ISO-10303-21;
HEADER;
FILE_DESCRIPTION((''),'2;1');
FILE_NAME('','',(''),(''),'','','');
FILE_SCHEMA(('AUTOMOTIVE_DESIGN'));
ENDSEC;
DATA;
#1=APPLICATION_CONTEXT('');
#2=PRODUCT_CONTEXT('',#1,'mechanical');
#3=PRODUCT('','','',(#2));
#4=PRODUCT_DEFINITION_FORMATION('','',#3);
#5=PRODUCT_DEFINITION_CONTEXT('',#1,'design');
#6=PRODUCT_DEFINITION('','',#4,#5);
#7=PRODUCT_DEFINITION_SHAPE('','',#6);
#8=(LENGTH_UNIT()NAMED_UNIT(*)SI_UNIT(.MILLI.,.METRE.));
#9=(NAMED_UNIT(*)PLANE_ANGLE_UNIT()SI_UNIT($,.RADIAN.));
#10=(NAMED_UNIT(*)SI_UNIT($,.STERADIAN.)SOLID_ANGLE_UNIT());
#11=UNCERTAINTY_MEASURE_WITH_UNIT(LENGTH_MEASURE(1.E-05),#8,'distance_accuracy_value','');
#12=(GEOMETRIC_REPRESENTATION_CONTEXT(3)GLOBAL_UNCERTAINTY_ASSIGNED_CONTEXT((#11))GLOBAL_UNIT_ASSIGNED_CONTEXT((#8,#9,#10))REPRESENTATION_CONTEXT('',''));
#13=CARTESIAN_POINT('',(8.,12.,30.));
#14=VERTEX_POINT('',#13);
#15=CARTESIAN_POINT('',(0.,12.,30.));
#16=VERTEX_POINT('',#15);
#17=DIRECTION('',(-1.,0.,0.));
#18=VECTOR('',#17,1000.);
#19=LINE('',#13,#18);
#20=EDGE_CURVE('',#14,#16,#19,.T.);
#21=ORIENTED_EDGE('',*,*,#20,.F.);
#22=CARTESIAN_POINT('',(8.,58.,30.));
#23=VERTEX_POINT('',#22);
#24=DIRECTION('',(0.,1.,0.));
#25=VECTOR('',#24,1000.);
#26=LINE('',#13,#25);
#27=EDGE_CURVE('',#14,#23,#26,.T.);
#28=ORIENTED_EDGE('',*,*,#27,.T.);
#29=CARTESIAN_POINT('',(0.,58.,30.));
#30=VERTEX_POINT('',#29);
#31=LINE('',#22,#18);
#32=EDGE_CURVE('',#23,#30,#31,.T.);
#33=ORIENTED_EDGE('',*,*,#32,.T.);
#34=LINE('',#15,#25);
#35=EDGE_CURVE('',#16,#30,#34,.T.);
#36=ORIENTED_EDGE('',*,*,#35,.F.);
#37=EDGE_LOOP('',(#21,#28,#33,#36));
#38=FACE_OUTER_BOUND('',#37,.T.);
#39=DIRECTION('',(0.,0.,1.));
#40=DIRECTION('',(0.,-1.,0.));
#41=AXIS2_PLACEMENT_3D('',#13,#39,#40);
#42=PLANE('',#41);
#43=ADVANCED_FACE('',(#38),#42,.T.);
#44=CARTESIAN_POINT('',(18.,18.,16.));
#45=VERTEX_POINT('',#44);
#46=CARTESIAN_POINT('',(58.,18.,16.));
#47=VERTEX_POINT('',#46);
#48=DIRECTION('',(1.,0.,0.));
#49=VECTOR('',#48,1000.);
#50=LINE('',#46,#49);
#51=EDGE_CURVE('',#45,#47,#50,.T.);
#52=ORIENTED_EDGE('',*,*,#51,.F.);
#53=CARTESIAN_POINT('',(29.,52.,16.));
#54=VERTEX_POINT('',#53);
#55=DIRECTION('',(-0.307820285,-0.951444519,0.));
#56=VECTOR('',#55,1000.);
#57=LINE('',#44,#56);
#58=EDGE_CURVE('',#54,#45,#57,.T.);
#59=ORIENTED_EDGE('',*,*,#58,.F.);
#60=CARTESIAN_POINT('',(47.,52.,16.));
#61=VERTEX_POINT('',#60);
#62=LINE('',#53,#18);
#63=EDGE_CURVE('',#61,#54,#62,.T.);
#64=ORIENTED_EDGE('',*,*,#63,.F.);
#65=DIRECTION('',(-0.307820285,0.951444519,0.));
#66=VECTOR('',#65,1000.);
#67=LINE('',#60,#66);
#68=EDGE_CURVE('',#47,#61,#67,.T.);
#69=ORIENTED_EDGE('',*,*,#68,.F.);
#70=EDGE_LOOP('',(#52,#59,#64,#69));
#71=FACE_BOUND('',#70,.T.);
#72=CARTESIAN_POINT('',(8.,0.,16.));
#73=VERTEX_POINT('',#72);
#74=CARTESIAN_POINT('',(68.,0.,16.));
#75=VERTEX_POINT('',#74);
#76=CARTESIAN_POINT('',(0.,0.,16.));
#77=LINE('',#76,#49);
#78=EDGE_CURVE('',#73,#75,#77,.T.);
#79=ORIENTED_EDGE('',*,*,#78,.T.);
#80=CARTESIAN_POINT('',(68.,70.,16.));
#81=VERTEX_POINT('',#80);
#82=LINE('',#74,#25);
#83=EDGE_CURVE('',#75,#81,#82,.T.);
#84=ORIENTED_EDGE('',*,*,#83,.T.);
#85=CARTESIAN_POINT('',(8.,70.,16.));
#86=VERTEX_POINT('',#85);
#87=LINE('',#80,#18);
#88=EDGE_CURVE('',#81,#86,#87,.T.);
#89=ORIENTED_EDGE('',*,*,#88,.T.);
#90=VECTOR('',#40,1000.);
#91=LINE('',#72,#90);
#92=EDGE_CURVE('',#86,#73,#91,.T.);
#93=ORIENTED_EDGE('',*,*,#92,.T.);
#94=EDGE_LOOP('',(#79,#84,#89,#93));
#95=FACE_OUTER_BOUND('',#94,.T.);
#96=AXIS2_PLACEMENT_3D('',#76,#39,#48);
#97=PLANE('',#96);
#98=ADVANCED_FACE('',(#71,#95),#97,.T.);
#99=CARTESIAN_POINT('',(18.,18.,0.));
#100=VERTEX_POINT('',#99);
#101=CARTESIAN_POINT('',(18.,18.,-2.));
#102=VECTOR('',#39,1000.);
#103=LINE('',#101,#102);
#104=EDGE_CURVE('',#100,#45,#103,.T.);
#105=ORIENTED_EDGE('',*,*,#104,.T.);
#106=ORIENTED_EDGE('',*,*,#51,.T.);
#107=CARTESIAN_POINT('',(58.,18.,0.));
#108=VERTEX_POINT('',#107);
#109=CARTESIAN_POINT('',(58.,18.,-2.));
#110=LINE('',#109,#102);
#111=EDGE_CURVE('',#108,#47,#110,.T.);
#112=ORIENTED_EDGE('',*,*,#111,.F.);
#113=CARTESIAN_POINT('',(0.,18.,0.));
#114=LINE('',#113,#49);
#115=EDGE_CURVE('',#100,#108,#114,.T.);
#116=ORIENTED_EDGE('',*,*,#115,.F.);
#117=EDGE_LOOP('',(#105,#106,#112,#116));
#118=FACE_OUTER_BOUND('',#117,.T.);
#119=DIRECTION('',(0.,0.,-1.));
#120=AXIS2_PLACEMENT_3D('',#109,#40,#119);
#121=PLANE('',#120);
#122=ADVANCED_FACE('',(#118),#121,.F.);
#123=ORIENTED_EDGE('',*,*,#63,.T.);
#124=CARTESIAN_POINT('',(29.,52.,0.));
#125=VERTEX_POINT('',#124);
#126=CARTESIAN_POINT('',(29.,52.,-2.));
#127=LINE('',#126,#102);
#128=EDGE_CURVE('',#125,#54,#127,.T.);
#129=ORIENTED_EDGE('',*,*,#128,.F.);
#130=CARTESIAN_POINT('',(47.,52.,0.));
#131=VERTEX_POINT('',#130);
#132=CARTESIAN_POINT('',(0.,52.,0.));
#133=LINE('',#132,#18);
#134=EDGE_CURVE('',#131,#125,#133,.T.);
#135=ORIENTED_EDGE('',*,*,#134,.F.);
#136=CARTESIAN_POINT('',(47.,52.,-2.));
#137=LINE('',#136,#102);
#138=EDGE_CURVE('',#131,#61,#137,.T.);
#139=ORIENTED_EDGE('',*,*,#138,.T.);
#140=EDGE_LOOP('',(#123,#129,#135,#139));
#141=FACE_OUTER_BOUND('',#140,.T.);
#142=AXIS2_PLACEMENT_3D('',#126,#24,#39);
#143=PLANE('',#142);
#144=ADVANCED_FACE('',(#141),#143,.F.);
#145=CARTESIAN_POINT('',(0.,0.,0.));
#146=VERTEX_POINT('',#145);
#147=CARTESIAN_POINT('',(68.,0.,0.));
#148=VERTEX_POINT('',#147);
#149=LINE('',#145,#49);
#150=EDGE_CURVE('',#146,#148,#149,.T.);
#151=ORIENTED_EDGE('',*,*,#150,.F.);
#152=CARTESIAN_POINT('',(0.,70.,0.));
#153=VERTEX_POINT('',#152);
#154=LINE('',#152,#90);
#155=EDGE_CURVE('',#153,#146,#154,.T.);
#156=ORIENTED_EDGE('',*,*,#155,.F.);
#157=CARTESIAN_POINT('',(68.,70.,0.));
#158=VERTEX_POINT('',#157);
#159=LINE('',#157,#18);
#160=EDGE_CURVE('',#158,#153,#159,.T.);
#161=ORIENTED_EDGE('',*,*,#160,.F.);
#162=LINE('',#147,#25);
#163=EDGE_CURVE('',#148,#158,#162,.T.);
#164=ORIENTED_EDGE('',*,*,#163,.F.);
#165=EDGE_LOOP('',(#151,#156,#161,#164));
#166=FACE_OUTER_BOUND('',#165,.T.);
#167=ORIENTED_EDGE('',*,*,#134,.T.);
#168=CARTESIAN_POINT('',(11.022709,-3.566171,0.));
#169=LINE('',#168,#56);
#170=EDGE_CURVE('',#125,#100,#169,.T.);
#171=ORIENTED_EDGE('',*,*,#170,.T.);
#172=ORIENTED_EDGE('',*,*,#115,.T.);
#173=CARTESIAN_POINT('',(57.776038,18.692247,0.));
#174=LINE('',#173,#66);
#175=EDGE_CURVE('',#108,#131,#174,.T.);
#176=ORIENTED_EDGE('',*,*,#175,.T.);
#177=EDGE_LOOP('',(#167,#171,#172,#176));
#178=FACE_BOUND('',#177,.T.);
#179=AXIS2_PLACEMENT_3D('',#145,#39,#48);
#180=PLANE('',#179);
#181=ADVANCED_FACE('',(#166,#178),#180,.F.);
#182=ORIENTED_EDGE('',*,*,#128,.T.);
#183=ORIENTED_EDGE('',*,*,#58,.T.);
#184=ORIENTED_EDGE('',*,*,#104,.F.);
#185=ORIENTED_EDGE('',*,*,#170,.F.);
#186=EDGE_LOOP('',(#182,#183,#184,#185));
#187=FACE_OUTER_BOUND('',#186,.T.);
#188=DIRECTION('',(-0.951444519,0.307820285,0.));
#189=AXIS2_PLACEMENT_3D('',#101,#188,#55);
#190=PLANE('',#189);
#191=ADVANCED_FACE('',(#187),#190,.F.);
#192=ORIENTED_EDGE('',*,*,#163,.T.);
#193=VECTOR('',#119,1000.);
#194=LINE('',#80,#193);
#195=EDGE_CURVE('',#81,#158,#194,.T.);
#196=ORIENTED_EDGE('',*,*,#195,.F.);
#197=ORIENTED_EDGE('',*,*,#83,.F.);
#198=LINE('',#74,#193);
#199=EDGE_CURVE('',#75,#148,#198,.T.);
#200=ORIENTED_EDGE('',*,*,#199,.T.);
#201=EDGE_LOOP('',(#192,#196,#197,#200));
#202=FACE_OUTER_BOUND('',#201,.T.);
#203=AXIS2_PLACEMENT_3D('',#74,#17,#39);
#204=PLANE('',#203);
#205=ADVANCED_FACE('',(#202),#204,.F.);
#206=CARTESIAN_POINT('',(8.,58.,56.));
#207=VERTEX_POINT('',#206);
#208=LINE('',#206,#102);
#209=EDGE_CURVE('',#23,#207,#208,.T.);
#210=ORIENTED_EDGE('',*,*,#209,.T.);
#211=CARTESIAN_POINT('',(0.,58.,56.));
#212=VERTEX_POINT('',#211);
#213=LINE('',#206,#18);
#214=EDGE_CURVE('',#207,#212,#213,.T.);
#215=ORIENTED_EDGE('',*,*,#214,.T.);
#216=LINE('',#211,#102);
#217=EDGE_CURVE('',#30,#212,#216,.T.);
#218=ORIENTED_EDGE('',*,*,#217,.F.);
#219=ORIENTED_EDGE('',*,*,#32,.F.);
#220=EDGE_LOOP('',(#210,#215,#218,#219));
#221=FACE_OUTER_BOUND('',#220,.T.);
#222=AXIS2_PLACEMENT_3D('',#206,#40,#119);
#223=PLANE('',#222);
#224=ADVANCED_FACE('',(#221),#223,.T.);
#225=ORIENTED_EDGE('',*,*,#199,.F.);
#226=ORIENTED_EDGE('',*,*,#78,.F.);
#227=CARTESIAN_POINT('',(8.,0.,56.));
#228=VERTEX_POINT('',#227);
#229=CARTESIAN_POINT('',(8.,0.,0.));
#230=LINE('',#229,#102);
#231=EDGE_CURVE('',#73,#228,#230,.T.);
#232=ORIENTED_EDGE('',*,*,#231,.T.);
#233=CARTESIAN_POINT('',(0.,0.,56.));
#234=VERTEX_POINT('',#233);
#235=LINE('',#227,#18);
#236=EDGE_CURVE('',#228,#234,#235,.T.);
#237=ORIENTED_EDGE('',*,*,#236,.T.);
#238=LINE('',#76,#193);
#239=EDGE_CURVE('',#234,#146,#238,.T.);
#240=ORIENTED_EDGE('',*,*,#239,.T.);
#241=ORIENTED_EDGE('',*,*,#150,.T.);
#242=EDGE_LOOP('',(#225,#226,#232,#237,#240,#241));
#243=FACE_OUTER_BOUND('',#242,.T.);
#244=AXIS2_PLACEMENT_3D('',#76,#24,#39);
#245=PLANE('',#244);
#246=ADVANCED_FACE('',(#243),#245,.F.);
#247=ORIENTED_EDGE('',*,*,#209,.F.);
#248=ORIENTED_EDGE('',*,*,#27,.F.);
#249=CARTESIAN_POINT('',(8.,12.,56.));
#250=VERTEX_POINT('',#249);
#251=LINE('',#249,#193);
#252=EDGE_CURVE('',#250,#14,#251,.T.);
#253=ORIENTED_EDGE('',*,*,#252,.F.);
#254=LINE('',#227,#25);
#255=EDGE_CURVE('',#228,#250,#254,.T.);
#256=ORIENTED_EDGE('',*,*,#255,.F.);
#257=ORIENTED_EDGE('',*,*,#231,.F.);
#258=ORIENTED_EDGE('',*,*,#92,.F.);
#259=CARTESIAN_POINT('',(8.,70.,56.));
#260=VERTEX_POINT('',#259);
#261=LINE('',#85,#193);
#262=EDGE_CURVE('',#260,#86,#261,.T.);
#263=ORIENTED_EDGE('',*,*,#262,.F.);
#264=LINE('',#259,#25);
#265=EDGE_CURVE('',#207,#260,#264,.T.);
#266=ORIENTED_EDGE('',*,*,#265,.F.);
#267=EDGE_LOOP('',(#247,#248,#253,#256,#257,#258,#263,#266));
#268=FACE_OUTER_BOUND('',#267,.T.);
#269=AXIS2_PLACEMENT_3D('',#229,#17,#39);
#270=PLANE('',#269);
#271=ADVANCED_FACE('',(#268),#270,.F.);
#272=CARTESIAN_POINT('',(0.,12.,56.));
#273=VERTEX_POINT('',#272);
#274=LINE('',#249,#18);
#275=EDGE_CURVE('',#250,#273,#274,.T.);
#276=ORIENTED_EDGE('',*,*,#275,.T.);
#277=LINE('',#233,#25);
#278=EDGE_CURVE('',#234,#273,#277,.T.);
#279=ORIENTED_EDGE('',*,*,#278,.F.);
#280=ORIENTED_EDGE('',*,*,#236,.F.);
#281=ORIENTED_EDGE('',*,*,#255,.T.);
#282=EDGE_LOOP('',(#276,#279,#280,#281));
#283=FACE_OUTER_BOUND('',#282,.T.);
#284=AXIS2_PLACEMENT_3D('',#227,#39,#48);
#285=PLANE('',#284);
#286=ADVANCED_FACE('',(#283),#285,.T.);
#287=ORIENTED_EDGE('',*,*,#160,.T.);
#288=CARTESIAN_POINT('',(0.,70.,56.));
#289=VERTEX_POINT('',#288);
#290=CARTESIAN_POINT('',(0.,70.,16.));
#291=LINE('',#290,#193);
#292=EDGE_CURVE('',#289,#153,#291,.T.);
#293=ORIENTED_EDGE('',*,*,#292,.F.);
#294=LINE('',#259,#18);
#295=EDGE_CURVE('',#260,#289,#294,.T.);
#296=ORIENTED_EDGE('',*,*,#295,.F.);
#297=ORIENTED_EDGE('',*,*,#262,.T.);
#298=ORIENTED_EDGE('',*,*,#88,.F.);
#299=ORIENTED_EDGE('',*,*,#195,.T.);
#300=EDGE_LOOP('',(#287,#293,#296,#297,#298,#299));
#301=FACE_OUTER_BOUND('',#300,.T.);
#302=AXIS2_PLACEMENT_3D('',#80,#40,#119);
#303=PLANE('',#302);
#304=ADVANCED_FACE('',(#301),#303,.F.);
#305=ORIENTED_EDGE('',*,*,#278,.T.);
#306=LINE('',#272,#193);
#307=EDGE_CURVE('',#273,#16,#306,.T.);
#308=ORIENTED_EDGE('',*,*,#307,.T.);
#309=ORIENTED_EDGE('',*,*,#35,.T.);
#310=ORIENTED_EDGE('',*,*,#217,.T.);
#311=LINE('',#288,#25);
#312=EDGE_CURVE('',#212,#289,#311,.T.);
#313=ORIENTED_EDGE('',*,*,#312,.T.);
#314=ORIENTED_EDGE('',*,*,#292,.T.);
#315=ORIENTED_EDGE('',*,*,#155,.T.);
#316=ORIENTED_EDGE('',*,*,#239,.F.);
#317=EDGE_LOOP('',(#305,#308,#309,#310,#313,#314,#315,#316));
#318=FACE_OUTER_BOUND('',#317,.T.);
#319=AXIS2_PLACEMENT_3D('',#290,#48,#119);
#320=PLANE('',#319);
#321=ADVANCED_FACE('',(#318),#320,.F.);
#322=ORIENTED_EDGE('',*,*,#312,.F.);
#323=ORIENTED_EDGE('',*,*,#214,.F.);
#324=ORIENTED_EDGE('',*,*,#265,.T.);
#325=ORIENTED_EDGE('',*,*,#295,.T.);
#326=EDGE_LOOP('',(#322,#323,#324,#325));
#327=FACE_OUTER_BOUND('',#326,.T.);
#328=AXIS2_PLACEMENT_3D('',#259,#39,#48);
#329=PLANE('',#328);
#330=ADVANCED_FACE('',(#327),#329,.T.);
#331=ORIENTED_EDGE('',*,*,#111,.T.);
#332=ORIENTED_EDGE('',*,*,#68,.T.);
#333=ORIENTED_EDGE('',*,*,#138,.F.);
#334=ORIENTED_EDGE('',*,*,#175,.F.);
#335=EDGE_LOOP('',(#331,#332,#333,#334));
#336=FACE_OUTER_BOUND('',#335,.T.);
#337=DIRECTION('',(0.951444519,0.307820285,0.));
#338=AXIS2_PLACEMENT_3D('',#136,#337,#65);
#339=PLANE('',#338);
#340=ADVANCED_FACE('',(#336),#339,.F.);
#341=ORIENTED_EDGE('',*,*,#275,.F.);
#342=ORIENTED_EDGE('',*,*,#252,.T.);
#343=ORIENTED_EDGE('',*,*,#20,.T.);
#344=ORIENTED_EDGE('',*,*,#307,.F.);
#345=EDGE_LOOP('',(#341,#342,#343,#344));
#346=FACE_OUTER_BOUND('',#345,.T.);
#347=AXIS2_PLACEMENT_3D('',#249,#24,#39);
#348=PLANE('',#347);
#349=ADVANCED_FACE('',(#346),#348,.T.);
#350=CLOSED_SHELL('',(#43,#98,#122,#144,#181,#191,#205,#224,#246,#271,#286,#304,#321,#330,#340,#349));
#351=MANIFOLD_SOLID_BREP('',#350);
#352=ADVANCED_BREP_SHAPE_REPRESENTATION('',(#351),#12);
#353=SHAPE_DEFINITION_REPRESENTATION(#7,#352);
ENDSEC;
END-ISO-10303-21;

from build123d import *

# Parameters (mm, degrees)
BASE_PLATE_SKETCH_W     = 68
BASE_PLATE_SKETCH_H     = 70
BASE_PLATE_16MM_DEPTH   = 16
C_SIDE_FLANGE_8MM_DEPTH = 8
WINDOW_CUT_OUT_DEPTH    = 18


with BuildPart() as part:
    # Base Plate Sketch → Base Plate 16mm (new body)
    with BuildSketch(Plane.XY):
        with Locations((34, 35)):
            Rectangle(BASE_PLATE_SKETCH_W, BASE_PLATE_SKETCH_H)
    extrude(amount=BASE_PLATE_16MM_DEPTH)

    # Side Flange Sketch → C Side Flange 8mm (add)
    with BuildSketch(Plane.ZY):
        Polygon((16, 70), (56, 70), (56, 58), (30, 58), (30, 12), (56, 12), (56, 0), (16, 0), (0, 0), (0, 70), align=None)
    extrude(amount=-C_SIDE_FLANGE_8MM_DEPTH)

    # Window Sketch → Window Cut-Out (cut)
    with BuildSketch(Plane.XY.offset(16)):
        Polygon((58, 18), (18, 18), (29, 52), (38, 52), (47, 52), align=None)
    extrude(amount=-WINDOW_CUT_OUT_DEPTH, mode=Mode.SUBTRACT)


solid = part.part
